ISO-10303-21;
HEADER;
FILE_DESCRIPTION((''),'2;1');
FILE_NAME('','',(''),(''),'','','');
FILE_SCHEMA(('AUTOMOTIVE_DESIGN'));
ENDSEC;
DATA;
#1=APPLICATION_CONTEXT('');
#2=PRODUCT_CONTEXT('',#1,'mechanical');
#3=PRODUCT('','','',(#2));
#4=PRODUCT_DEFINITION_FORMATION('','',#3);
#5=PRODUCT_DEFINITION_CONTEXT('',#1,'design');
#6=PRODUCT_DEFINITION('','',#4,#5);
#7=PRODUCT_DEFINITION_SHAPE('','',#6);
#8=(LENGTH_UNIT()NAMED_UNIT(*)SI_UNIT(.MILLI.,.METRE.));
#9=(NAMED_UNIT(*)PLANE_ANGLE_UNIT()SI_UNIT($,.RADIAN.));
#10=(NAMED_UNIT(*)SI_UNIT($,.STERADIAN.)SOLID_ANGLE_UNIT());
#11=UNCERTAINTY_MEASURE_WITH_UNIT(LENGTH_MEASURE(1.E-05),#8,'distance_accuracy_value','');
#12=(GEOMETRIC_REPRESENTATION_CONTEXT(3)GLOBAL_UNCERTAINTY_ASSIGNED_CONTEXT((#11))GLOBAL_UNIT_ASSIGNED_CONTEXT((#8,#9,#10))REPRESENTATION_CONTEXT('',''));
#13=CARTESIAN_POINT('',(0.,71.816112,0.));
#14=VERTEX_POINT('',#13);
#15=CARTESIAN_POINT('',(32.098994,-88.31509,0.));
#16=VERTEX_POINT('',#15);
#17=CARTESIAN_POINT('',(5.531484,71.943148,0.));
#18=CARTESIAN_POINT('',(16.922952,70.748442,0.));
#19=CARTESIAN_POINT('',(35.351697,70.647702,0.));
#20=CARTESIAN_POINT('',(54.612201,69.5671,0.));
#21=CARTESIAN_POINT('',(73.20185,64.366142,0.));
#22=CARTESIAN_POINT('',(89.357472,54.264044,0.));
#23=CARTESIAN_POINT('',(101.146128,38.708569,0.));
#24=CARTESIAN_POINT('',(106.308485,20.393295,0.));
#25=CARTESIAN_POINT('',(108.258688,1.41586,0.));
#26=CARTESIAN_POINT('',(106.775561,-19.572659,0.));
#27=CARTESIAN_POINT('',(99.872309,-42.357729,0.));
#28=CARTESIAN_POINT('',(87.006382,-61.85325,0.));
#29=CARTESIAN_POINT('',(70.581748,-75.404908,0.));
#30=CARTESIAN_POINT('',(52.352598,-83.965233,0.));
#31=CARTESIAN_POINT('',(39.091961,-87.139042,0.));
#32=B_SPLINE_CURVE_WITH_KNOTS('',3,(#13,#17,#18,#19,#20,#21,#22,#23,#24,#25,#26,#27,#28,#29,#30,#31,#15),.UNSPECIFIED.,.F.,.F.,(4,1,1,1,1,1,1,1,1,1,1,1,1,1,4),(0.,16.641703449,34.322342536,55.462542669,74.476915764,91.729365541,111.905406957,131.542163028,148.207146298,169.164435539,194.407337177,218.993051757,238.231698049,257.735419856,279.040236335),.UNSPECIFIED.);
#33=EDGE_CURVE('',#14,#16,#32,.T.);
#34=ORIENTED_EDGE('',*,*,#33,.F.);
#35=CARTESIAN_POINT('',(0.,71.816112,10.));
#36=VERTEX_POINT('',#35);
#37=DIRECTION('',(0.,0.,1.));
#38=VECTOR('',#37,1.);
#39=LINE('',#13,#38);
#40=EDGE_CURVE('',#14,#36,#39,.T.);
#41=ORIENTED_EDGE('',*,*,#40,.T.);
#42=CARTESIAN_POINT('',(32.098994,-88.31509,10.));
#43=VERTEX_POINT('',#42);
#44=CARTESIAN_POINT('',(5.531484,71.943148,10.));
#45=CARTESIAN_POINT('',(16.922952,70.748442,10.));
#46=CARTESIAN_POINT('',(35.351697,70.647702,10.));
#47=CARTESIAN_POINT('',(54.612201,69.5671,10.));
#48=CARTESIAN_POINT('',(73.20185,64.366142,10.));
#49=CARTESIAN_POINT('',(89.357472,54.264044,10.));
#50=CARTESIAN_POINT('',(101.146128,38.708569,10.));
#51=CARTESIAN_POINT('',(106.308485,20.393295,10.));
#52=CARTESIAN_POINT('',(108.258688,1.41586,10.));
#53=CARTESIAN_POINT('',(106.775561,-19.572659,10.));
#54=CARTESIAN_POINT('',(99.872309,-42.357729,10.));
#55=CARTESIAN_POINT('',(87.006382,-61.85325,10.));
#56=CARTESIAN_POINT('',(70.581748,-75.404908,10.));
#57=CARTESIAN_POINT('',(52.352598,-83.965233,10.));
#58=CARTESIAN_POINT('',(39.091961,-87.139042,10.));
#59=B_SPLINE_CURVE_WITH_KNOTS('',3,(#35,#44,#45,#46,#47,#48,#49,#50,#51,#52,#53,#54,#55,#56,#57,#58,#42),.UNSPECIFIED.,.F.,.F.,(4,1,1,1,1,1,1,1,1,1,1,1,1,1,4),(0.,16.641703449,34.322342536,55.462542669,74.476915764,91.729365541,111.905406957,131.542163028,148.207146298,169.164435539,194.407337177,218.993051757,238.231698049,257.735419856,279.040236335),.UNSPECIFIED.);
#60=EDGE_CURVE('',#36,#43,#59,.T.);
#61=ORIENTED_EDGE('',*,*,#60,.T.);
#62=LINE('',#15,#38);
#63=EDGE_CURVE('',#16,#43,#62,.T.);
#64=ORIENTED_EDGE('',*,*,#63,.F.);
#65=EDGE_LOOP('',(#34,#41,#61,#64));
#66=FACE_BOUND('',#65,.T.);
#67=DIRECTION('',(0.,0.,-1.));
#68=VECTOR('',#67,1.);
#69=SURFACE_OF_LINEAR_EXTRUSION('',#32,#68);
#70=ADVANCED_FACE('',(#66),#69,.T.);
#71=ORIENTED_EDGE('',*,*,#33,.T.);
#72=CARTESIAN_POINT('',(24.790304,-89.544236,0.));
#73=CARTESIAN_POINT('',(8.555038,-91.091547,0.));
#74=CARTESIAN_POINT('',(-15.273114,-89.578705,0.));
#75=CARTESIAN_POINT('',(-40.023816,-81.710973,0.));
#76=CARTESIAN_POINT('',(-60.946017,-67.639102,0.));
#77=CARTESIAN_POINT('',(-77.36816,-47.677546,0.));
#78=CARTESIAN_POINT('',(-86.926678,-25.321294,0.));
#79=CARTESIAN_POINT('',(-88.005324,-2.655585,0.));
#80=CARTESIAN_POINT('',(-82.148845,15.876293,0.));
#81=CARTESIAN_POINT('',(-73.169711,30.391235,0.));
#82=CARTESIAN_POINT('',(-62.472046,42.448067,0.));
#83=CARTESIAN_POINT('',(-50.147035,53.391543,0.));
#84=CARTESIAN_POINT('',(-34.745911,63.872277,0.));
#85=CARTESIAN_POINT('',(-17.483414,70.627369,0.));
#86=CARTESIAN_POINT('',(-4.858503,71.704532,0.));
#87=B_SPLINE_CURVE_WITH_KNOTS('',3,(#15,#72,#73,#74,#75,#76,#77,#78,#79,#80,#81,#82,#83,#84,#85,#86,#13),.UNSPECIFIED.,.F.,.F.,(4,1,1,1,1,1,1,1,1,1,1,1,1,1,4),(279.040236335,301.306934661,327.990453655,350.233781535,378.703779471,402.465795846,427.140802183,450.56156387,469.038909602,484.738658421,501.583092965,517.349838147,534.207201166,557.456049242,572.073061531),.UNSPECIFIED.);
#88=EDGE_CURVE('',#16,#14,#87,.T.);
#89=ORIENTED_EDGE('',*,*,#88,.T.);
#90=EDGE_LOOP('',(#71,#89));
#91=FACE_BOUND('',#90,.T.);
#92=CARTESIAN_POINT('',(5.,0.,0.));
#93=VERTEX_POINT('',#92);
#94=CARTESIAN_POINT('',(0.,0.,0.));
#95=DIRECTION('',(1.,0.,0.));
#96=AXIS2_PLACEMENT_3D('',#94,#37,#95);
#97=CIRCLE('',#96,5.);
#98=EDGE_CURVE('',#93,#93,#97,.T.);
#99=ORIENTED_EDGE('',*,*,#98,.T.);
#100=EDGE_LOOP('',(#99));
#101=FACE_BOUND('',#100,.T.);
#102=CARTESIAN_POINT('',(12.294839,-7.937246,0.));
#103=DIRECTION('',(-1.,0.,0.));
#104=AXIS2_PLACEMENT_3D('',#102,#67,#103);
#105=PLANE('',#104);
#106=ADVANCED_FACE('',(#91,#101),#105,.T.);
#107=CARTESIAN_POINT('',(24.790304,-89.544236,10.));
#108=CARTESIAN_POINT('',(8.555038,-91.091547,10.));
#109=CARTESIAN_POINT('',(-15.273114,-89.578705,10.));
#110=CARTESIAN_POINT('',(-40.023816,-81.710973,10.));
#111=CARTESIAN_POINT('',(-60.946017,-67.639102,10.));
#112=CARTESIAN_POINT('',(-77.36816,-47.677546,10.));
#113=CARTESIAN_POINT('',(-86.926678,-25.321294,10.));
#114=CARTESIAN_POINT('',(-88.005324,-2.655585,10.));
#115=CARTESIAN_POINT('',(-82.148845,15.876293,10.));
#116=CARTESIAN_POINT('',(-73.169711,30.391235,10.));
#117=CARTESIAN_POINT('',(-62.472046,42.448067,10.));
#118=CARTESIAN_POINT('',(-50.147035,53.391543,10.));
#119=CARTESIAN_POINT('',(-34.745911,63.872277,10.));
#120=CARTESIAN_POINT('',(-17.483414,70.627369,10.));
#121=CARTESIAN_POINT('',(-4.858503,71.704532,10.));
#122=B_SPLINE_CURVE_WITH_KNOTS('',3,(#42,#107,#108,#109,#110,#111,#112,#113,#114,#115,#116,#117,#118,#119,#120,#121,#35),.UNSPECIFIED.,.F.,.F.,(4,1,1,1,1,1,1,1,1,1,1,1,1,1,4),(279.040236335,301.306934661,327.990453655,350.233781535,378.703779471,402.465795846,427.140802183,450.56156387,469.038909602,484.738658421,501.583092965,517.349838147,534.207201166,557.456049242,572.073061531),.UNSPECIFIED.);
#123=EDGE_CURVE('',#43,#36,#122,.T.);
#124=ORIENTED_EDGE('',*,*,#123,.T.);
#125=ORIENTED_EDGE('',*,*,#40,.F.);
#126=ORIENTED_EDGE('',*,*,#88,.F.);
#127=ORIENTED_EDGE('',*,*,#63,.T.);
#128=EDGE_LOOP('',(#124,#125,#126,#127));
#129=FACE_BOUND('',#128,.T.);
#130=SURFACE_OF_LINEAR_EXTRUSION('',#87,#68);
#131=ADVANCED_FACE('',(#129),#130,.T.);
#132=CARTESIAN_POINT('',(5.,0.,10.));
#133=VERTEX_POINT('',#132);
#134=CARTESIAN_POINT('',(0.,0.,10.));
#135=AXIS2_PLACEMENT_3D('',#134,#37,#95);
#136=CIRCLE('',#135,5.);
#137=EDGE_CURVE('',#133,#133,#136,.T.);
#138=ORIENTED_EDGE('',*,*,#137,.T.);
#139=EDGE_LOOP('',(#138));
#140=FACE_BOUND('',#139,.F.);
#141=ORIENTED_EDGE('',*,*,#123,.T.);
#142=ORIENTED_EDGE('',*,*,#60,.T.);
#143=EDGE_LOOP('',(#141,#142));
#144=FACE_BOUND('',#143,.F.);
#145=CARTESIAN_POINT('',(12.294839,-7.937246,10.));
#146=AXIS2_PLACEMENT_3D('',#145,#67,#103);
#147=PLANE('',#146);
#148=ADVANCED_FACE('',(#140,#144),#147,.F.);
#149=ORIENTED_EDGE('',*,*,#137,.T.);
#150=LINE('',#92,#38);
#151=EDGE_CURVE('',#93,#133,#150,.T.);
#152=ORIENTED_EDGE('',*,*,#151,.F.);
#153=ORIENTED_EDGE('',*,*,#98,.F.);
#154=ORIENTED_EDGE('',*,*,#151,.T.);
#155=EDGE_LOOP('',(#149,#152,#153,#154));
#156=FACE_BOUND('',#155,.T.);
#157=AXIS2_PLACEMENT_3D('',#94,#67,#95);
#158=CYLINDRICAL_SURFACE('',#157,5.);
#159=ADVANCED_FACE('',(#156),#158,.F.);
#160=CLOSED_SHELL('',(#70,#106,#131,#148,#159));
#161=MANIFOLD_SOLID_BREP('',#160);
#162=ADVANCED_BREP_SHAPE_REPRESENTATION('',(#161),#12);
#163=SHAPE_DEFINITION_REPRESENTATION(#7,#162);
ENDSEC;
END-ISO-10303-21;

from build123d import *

# Parameters (mm, degrees)
SKETCH3_R           = 5
BOSS_EXTRUDE1_DEPTH = 10


with BuildPart() as part:
    # Sketch3 → Boss-Extrude1 (new body)
    with BuildSketch(Plane.XY):
        with BuildLine():
            add(Edge.make_bspline(
                [(32.098993714, -88.315090172), (24.790304353, -89.544235685), (8.555038023, -91.091547174), (-15.273114308, -89.578704931), (-40.023815861, -81.710972799), (-60.94601733, -67.639101592), (-77.368159975, -47.677546318), (-86.926677755, -25.321294301), (-88.005324434, -2.655584715), (-82.148845494, 15.87629255), (-73.16971112, 30.391235296), (-62.472045739, 42.448066508), (-50.147034888, 53.39154317), (-34.745911271, 63.872277011), (-17.483414176, 70.627368849), (-4.858503178, 71.704531936), (0, 71.816111973)],
                knots=[279.040236335, 279.040236335, 279.040236335, 279.040236335, 301.306934661, 327.990453655, 350.233781535, 378.703779471, 402.465795846, 427.140802183, 450.56156387, 469.038909602, 484.738658421, 501.583092965, 517.349838147, 534.207201166, 557.456049242, 572.073061531, 572.073061531, 572.073061531, 572.073061531], degree=3, weights=[1, 1, 1, 1, 1, 1, 1, 1, 1, 1, 1, 1, 1, 1, 1, 1, 1]))
            add(Edge.make_bspline(
                [(0, 71.816111973), (5.53148395, 71.943147639), (16.922952207, 70.74844157), (35.351697322, 70.647702193), (54.612200678, 69.567100223), (73.20185028, 64.366142209), (89.357471879, 54.264044334), (101.146128347, 38.708568873), (106.308485454, 20.393294593), (108.258687784, 1.415860382), (106.775560538, -19.572658629), (99.872309139, -42.357728983), (87.006382252, -61.853250376), (70.581747793, -75.404908213), (52.352597958, -83.965233493), (39.091960666, -87.139041564), (32.098993714, -88.315090172)],
                knots=[0, 0, 0, 0, 16.641703449, 34.322342536, 55.462542669, 74.476915764, 91.729365541, 111.905406957, 131.542163028, 148.207146298, 169.164435539, 194.407337177, 218.993051757, 238.231698049, 257.735419856, 279.040236335, 279.040236335, 279.040236335, 279.040236335], degree=3, weights=[1, 1, 1, 1, 1, 1, 1, 1, 1, 1, 1, 1, 1, 1, 1, 1, 1]))
        make_face()
        Circle(SKETCH3_R, mode=Mode.SUBTRACT)
    extrude(amount=BOSS_EXTRUDE1_DEPTH)


solid = part.part
